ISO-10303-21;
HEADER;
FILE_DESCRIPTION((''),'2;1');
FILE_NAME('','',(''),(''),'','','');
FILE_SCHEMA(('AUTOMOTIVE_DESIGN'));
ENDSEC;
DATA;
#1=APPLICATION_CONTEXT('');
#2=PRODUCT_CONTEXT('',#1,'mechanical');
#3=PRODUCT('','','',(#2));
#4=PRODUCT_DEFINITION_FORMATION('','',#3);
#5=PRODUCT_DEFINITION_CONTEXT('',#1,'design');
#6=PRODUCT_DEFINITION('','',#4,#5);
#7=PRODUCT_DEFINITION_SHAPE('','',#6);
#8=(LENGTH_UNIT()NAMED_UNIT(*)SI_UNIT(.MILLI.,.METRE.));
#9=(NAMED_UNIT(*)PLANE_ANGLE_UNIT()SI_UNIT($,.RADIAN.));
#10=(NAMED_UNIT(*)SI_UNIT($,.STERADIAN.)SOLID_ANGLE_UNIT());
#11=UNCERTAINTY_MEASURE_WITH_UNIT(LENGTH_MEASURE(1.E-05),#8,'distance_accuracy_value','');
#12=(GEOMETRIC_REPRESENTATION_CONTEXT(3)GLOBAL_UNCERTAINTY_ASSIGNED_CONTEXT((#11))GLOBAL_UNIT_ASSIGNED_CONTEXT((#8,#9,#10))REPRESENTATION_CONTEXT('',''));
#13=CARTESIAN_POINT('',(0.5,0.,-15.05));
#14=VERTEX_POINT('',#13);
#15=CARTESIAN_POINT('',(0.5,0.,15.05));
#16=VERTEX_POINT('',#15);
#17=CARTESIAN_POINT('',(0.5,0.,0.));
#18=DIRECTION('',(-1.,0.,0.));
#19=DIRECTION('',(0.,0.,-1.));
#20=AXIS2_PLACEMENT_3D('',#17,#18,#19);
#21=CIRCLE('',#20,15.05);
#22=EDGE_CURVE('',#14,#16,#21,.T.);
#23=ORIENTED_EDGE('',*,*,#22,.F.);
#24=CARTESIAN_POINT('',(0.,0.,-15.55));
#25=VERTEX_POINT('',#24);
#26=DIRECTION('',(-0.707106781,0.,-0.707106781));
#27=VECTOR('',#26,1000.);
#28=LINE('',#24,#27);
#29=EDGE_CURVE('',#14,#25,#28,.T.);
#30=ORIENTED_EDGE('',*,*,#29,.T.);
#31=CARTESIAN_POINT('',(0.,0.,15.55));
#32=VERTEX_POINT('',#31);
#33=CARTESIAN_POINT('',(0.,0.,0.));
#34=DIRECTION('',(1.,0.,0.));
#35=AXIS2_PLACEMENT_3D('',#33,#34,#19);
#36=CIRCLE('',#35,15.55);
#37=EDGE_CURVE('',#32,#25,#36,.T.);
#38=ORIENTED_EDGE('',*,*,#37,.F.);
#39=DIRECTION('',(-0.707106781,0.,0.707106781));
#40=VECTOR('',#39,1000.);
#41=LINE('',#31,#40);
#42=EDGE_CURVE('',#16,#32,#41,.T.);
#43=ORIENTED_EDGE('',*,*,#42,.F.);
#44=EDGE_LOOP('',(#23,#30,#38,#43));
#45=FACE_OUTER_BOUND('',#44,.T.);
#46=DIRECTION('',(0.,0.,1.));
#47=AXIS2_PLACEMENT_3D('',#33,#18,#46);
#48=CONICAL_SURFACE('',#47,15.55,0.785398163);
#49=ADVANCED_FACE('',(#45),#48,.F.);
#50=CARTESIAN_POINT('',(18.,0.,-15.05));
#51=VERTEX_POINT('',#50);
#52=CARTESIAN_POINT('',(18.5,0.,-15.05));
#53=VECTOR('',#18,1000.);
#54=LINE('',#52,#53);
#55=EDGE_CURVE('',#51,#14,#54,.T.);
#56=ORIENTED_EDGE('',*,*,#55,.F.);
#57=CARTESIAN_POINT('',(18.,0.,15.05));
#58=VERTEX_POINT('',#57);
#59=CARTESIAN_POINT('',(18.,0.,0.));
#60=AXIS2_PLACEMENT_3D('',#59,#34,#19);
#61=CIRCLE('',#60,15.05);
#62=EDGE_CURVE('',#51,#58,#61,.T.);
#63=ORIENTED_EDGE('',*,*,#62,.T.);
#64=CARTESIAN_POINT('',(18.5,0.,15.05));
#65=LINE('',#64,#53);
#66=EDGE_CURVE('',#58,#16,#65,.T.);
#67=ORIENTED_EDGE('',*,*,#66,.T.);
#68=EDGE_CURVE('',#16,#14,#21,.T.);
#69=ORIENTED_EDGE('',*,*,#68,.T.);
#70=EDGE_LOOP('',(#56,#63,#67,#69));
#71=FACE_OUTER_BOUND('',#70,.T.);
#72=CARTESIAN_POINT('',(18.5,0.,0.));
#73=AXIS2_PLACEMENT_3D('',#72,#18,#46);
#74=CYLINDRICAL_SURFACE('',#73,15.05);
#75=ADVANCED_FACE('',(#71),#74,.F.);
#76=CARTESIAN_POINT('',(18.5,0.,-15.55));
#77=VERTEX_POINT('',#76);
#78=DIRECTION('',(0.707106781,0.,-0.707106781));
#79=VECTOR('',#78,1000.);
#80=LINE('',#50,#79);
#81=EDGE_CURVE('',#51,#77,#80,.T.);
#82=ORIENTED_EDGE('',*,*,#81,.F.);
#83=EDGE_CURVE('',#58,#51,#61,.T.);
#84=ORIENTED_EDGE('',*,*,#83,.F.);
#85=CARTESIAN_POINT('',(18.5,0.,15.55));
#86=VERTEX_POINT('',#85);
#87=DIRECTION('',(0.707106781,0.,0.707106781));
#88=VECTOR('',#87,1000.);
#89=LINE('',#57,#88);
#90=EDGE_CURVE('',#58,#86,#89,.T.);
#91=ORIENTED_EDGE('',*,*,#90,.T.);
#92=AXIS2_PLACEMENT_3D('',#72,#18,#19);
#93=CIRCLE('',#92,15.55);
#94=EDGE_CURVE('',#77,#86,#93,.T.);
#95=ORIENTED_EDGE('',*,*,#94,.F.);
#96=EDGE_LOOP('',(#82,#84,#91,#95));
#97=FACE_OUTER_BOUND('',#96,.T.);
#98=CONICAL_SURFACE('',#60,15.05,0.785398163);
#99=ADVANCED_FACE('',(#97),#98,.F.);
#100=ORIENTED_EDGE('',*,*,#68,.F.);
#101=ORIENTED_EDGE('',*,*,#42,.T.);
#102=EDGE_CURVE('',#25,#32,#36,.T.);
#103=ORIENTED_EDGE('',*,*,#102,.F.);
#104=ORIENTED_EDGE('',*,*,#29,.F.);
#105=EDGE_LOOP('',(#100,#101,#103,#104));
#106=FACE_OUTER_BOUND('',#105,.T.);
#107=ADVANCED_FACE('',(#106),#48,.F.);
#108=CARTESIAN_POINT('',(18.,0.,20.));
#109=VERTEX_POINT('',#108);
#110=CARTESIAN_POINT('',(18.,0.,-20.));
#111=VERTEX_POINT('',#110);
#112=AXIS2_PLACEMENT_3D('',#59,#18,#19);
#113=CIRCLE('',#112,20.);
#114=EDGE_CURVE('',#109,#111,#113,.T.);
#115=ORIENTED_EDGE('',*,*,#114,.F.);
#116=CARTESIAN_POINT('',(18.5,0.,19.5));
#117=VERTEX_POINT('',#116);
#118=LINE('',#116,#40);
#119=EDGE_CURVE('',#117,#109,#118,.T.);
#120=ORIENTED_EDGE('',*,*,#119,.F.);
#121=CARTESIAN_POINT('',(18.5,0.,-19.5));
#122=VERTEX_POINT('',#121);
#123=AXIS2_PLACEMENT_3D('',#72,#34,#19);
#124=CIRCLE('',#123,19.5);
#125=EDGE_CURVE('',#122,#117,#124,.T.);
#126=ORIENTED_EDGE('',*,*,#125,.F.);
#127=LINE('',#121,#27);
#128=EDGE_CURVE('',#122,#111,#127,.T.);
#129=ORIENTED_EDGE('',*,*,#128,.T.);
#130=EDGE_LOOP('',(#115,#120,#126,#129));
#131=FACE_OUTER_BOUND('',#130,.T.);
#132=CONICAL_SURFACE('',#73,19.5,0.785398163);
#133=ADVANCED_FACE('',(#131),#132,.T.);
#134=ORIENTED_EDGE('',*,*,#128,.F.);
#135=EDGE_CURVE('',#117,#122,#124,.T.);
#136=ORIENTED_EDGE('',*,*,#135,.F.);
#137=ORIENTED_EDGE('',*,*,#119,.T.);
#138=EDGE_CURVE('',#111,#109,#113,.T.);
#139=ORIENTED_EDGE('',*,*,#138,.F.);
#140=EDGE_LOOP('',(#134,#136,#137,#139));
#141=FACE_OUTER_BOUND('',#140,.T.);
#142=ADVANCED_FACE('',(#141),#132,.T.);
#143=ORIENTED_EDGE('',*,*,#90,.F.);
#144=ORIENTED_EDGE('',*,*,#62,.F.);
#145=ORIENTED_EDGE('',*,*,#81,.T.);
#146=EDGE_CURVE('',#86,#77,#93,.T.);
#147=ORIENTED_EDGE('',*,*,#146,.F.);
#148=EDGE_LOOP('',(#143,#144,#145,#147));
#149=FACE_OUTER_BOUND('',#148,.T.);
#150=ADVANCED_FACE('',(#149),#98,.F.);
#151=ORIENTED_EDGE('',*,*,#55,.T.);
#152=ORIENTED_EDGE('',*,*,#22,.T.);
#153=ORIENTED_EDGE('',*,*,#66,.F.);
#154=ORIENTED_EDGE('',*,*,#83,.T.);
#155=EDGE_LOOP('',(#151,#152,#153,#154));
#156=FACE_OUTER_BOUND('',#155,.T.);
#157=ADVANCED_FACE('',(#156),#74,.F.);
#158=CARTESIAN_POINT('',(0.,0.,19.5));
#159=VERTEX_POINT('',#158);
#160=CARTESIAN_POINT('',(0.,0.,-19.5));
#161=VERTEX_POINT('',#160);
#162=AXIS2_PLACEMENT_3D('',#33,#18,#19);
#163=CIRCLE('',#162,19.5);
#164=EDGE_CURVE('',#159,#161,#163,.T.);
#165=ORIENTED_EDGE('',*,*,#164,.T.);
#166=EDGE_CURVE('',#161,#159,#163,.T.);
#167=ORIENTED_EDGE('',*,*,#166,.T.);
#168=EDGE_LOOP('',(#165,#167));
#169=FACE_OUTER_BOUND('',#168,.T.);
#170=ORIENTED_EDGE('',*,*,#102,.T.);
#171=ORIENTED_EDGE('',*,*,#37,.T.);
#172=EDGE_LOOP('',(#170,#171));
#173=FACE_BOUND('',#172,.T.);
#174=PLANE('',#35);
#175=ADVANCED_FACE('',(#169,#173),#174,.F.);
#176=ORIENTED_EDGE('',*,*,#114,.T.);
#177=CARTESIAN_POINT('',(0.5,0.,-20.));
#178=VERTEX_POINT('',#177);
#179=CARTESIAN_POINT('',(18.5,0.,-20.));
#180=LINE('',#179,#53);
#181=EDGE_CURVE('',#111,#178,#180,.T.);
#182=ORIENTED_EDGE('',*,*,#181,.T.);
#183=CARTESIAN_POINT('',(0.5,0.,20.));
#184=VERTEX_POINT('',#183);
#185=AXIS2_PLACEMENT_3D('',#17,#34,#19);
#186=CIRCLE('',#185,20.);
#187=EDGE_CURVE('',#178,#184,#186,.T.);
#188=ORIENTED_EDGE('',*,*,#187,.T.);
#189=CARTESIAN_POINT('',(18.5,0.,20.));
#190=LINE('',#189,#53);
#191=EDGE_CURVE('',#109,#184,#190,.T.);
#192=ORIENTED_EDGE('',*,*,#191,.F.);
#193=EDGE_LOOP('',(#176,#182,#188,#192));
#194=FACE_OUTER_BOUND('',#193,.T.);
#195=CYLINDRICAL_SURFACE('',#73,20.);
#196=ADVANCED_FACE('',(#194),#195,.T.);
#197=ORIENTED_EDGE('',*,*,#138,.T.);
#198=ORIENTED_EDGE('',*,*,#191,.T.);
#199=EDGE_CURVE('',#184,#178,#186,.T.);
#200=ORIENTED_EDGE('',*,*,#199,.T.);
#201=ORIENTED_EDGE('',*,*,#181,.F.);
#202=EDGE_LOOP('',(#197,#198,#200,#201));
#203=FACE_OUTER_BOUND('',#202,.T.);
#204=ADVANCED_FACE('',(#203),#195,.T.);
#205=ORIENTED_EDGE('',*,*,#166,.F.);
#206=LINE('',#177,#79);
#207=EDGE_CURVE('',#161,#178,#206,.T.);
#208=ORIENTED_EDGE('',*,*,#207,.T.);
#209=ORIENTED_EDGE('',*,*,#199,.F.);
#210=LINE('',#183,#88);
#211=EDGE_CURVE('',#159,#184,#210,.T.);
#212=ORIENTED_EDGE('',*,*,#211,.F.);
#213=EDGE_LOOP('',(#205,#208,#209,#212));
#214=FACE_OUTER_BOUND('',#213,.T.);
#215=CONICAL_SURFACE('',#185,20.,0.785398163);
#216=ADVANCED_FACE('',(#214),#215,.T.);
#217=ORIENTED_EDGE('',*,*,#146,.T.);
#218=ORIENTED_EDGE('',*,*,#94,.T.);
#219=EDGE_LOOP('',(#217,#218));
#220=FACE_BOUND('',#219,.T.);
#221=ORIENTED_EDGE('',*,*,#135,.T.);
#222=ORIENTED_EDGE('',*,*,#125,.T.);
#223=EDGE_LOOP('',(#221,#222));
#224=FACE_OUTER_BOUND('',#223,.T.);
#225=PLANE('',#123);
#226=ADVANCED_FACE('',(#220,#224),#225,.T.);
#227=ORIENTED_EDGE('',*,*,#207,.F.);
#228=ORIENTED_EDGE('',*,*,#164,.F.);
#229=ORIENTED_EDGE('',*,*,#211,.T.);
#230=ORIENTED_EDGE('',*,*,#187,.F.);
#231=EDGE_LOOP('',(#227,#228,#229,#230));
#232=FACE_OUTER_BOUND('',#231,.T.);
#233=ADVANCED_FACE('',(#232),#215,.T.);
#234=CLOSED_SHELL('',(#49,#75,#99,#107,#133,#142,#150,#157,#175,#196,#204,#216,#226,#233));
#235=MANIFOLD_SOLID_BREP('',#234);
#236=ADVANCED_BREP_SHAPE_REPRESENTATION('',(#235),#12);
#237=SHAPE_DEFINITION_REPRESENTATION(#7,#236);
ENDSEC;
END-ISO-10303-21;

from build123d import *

# Parameters (mm, degrees)
SKETCH_1_R      = 20
SKETCH_1_R_2    = 15.05
EXTRUDE_1_DEPTH = 18.5
CHAMFER_1_SIZE  = 0.5


with BuildPart() as part:
    # 草图1 → 凸台-拉伸1 (new body)
    with BuildSketch(Plane(origin=(0, 0, 0), x_dir=(0, 0, -1), z_dir=(1, 0, 0))):
        Circle(SKETCH_1_R)
        Circle(SKETCH_1_R_2, mode=Mode.SUBTRACT)
    extrude(amount=EXTRUDE_1_DEPTH)

    # 倒角1
    chamfer_1_edges = [part.edges().sort_by_distance(p)[0] for p in [
        (0, 0, 20),
        (18.5, 0, 20),
        (0, 0, 15.05),
        (18.5, 0, 15.05),
    ]]
    chamfer(chamfer_1_edges, length=CHAMFER_1_SIZE)


solid = part.part
